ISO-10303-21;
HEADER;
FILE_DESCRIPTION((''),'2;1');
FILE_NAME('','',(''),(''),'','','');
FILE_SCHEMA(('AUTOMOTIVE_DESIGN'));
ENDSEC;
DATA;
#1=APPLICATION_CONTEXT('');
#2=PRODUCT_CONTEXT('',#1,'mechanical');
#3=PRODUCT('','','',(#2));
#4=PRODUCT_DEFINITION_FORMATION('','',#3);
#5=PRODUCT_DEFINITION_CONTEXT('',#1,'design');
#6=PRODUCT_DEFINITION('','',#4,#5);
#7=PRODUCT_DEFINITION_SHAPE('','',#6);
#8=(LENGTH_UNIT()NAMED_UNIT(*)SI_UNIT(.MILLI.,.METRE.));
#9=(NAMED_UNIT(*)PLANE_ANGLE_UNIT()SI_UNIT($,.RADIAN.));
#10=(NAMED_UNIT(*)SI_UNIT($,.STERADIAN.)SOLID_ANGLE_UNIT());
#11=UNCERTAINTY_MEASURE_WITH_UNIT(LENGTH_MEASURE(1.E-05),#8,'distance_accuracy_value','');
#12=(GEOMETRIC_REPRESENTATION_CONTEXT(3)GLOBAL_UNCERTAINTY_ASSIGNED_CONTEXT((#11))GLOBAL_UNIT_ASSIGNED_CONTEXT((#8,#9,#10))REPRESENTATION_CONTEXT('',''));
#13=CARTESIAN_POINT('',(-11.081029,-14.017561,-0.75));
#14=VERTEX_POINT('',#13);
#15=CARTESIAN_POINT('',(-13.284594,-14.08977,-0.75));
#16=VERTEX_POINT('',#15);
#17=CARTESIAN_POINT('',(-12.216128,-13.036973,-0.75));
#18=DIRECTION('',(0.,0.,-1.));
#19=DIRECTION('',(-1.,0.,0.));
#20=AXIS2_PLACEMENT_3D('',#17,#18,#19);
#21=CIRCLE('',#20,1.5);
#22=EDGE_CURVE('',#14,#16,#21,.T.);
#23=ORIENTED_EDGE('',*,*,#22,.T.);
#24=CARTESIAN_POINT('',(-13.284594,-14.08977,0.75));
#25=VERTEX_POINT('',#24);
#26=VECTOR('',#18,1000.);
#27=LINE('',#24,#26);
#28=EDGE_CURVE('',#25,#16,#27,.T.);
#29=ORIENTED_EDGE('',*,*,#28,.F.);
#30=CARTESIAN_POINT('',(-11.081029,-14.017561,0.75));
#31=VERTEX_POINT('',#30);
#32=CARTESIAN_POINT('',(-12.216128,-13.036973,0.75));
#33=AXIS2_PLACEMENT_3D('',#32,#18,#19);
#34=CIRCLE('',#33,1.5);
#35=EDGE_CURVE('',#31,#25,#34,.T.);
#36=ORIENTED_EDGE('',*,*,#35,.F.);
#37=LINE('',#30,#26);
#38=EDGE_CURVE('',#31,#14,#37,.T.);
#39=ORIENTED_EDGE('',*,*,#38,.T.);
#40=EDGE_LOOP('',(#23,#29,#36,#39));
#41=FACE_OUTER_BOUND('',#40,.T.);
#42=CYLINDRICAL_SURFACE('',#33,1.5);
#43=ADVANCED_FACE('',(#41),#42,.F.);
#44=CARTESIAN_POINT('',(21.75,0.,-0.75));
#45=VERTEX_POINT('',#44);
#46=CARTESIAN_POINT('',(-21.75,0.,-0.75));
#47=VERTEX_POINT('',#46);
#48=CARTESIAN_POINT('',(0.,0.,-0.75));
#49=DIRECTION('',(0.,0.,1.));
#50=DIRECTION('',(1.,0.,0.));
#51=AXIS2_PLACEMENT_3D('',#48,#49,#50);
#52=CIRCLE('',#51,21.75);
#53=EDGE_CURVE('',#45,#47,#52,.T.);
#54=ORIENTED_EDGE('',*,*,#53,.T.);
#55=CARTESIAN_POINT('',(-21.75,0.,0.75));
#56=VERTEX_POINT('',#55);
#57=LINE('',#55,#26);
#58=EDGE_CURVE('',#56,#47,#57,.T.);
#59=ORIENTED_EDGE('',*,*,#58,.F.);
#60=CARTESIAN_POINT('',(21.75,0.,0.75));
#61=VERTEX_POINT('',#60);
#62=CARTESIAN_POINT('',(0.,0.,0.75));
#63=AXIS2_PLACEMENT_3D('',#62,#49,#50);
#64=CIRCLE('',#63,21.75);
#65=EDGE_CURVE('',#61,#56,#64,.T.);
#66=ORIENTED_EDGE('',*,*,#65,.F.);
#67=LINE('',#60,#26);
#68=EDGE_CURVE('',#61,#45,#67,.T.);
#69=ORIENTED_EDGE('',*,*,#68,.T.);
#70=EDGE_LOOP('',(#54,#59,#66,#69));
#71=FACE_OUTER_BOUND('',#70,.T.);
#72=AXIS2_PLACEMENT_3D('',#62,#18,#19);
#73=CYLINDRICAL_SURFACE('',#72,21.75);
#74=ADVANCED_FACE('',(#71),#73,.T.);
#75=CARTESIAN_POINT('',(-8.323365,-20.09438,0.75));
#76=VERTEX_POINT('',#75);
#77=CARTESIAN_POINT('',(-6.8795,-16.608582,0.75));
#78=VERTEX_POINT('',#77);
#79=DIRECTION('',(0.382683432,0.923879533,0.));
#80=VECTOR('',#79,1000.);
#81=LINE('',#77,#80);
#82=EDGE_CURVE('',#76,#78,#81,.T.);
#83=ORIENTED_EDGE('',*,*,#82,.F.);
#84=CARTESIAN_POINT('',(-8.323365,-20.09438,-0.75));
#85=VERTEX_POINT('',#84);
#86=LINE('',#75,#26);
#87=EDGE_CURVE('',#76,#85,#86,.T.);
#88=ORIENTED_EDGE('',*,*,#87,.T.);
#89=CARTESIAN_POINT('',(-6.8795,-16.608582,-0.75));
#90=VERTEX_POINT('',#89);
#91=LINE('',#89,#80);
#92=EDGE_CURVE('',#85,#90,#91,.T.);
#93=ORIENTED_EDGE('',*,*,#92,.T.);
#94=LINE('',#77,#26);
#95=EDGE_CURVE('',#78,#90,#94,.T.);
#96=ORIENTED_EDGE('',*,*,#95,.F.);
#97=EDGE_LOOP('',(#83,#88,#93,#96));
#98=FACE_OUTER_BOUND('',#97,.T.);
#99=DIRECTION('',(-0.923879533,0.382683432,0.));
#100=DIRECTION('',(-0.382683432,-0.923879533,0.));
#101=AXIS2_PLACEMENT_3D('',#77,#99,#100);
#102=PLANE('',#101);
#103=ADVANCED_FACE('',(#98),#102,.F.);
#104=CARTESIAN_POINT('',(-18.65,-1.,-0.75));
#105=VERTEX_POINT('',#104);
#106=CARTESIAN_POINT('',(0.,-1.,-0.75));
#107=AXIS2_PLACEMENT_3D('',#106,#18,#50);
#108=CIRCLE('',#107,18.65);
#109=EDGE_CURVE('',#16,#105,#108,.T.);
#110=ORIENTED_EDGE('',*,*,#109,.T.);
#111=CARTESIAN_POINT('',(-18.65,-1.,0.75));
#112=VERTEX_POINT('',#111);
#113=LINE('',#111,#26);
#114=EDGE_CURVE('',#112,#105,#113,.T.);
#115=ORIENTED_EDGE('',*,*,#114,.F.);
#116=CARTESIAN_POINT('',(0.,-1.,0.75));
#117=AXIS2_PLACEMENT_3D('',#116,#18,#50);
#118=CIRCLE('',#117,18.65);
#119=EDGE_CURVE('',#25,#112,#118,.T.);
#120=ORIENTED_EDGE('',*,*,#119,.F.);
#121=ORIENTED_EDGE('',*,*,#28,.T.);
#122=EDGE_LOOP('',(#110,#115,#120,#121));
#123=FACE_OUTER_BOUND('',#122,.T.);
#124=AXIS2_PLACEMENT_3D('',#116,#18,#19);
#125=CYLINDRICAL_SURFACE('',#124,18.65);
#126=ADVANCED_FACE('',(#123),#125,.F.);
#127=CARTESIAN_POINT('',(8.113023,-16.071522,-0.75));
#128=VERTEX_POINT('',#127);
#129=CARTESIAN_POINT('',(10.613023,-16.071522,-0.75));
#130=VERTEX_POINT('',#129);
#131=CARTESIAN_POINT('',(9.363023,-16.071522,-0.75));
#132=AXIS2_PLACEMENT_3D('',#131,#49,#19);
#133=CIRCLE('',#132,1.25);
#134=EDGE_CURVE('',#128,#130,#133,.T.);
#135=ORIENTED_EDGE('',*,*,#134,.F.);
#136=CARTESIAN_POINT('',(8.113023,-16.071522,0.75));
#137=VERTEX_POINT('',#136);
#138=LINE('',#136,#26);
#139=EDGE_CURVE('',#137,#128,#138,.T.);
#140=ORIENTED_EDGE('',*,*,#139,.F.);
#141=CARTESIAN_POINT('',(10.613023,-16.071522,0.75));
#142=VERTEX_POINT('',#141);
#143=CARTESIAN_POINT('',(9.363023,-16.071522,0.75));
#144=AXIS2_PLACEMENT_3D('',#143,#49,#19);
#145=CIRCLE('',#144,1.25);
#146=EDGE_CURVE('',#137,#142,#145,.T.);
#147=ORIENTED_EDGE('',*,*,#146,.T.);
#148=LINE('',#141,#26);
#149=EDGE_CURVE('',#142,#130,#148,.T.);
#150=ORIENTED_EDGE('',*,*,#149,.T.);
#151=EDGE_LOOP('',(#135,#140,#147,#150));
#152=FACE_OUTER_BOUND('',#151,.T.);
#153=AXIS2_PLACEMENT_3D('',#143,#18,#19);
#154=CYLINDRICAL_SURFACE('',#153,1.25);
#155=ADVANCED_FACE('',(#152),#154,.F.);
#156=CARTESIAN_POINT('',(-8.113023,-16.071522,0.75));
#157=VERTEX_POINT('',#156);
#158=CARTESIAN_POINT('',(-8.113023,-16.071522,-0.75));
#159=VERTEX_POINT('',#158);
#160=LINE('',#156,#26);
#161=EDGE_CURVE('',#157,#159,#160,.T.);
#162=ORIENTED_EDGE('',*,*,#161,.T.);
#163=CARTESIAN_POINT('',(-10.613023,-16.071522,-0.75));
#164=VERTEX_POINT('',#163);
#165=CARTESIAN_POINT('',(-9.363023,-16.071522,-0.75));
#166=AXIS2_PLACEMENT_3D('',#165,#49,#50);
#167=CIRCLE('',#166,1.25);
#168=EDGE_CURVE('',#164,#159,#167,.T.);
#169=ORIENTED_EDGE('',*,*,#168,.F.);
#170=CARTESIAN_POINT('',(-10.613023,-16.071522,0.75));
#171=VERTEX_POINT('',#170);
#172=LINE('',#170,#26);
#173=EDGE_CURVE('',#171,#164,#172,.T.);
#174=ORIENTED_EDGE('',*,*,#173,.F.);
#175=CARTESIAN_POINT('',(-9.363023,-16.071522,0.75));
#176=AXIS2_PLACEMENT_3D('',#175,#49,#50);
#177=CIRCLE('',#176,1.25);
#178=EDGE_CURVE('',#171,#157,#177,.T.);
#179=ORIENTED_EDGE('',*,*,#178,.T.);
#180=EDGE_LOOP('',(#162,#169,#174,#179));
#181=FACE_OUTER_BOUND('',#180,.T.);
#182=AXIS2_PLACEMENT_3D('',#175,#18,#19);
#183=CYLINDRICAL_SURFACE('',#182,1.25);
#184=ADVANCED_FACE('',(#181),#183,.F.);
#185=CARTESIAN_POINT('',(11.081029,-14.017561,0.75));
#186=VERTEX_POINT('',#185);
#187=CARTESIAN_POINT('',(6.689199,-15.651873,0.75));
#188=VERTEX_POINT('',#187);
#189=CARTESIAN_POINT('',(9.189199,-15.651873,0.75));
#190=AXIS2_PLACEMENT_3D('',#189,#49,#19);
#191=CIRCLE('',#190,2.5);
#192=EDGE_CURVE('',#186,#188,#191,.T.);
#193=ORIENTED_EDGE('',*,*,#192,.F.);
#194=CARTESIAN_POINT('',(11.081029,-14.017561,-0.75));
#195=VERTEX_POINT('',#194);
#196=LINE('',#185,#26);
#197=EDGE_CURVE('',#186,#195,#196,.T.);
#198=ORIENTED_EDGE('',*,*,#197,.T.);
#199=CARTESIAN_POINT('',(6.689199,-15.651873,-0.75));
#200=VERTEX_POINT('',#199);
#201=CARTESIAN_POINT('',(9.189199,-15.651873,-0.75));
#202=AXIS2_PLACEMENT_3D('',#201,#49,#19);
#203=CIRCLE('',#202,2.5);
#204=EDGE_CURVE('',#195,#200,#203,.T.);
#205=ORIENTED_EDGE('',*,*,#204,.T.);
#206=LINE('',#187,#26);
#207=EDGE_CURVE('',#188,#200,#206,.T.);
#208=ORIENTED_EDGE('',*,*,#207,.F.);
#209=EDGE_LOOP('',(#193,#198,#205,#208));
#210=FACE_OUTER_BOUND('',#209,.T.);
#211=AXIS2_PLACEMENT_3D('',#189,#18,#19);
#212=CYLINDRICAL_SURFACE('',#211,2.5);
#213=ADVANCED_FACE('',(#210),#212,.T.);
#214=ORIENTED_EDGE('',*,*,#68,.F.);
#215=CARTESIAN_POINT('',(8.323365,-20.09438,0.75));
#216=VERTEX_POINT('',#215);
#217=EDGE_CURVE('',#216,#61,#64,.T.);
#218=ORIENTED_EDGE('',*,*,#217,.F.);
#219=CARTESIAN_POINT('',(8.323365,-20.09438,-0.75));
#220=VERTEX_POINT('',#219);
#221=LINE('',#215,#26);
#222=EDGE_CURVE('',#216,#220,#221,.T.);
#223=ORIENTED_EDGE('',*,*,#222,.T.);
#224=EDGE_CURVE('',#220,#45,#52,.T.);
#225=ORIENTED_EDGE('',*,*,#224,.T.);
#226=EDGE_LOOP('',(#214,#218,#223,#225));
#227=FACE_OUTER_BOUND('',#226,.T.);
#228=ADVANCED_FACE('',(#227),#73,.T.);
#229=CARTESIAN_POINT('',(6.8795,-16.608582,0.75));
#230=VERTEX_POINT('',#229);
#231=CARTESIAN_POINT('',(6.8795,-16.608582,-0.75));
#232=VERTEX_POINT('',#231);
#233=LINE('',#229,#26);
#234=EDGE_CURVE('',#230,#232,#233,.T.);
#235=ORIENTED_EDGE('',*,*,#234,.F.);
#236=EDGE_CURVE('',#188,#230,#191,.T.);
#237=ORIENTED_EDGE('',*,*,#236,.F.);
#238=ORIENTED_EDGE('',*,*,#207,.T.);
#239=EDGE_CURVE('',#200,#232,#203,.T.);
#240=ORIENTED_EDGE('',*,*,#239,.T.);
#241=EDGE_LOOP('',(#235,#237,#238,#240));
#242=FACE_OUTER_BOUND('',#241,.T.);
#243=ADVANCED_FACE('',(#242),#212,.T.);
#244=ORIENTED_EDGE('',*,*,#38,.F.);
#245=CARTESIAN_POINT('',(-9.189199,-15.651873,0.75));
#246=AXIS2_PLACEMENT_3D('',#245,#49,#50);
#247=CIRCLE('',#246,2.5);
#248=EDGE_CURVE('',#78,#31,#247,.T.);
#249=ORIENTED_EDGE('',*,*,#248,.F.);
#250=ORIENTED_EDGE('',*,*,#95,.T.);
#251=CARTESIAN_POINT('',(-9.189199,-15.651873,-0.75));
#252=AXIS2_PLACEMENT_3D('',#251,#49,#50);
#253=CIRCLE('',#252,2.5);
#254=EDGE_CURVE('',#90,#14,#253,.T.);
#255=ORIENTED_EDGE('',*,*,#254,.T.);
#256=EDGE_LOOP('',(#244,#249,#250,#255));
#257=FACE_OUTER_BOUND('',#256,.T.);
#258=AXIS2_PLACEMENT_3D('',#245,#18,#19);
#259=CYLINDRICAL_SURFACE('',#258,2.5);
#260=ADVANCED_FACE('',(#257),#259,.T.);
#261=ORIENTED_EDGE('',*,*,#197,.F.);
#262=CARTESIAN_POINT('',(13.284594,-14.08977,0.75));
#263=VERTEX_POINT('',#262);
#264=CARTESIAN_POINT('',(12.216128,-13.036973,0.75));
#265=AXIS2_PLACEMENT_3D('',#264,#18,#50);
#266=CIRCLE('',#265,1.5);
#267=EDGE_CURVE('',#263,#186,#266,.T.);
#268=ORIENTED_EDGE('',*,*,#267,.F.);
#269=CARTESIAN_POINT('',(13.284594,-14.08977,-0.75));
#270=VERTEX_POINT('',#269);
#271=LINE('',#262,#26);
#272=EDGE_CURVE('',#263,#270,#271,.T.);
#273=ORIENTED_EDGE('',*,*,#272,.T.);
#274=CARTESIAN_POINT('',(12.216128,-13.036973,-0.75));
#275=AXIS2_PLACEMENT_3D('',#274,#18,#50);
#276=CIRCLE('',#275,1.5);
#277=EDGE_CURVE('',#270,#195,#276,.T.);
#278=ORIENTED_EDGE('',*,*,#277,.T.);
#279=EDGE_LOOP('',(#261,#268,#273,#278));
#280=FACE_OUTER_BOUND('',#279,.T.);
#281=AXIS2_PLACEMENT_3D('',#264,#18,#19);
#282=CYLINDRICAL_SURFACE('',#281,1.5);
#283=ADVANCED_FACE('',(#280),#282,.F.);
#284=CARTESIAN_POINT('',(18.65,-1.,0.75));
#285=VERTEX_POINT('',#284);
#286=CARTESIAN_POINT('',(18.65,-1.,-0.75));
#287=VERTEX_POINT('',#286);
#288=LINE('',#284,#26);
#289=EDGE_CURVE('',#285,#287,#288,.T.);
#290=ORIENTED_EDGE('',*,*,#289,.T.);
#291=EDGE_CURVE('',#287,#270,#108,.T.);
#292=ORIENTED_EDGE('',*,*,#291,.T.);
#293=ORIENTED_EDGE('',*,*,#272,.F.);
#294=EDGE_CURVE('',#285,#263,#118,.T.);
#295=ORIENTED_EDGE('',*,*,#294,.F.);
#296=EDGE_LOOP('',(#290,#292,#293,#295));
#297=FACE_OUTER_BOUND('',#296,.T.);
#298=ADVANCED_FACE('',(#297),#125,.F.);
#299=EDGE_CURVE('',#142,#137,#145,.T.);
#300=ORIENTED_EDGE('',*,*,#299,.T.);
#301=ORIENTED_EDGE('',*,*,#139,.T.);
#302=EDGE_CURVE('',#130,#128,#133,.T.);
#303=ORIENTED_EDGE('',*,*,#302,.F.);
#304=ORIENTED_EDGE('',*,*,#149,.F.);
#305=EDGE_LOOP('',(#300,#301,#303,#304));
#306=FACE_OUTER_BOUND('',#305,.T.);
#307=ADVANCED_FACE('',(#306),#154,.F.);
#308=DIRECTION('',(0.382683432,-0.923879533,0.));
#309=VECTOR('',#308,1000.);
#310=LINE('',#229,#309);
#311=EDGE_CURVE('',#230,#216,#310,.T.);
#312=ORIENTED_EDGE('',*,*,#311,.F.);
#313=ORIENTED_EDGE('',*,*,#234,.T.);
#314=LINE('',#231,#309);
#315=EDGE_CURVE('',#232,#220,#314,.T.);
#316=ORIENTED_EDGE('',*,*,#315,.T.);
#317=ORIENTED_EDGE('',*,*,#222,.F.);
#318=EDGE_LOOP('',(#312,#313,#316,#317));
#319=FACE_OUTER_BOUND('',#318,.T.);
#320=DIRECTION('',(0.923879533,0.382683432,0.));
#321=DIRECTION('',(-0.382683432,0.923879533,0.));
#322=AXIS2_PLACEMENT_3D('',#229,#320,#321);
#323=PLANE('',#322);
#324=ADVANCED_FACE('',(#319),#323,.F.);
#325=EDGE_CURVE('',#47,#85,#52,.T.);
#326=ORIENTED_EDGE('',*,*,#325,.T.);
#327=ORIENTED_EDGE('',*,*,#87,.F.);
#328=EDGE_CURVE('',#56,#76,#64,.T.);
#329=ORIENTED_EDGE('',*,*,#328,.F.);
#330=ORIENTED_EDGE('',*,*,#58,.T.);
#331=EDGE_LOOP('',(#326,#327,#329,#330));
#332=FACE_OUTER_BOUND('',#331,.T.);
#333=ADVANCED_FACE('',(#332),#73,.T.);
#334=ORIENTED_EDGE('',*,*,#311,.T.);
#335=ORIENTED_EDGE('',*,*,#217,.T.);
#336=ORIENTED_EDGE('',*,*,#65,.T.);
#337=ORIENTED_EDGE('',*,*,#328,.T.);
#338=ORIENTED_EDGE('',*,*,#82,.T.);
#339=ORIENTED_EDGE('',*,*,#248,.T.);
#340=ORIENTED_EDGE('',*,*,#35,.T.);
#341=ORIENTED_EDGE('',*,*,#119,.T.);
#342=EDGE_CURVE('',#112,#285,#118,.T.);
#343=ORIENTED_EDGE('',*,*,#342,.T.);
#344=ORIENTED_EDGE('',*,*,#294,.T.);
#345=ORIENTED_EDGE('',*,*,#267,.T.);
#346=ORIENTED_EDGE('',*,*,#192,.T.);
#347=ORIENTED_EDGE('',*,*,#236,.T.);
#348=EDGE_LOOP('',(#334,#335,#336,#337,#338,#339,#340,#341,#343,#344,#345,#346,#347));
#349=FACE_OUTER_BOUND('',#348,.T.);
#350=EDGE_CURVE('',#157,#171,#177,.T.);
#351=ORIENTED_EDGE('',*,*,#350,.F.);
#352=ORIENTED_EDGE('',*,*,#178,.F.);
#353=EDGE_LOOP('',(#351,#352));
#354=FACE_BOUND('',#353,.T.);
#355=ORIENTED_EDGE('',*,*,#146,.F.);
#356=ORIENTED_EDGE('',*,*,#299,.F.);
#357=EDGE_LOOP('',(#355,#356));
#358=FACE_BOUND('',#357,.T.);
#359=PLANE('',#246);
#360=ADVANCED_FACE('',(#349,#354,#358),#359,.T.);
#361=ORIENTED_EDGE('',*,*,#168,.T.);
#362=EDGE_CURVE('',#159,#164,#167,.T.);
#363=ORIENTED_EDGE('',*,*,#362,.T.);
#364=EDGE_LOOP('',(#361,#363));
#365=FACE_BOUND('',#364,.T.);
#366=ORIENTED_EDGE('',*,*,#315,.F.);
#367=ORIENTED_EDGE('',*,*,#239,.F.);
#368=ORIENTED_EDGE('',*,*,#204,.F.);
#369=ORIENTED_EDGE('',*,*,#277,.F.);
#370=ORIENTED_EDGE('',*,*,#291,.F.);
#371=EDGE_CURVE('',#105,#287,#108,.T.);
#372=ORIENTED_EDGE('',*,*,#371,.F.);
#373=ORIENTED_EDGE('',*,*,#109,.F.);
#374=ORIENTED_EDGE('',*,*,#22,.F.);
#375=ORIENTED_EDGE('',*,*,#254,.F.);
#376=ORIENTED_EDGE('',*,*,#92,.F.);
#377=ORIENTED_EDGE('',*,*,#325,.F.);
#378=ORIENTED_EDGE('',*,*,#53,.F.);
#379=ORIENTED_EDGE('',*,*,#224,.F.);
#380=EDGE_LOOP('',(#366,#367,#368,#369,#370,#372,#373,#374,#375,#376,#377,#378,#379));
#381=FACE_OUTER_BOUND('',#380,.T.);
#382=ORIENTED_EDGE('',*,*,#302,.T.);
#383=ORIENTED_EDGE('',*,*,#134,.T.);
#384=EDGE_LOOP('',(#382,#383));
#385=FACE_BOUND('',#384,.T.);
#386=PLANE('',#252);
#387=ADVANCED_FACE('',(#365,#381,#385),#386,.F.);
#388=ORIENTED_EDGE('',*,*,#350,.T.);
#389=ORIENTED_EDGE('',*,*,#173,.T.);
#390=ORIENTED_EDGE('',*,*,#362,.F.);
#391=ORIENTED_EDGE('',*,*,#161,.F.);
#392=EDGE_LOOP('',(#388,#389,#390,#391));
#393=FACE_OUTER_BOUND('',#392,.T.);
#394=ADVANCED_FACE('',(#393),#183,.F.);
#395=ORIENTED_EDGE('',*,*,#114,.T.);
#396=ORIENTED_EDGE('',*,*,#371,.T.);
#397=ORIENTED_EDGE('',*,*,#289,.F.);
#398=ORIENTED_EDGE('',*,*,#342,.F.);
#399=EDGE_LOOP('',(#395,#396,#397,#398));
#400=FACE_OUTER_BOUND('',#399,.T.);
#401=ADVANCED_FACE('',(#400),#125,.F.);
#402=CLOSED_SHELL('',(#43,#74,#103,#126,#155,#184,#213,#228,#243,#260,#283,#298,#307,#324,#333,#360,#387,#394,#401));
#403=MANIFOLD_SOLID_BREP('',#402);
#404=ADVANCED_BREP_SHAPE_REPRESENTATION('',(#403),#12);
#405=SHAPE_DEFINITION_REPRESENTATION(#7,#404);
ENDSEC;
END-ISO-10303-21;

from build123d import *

# Parameters (mm, degrees)
EXTRUDE_962_DEPTH      = 0.75
EXTRUDE_962_DEPTH_BACK = 0.75
SKETCH_1_R             = 1.25


with BuildPart() as part:
    # 草图1 → Extrude 962 (new, two sides: drawn at the far end of the back side and taken through both)
    with BuildSketch(Plane.XY.offset(-EXTRUDE_962_DEPTH_BACK)):
        with BuildLine():
            Line((-6.879499755, -16.608581611), (-8.323364654, -20.094379832))
            ThreePointArc((-8.323364654, -20.094379832), (0, 21.75), (8.323364654, -20.094379832))
            Line((8.323364654, -20.094379832), (6.879499755, -16.608581611))
            ThreePointArc((6.879499755, -16.608581611), (7.876948304, -13.523963446), (11.081029231, -14.017560694))
            ThreePointArc((11.081029231, -14.017560694), (12.16700015, -14.536168573), (13.28459359, -14.08976979))
            ThreePointArc((13.28459359, -14.08976979), (0, 17.65), (-13.28459359, -14.08976979))
            ThreePointArc((-13.28459359, -14.08976979), (-12.16700015, -14.536168573), (-11.081029231, -14.017560694))
            ThreePointArc((-11.081029231, -14.017560694), (-7.876948304, -13.523963446), (-6.879499755, -16.608581611))
        make_face()
        with Locations((-9.363022706, -16.071521577)):
            Circle(SKETCH_1_R, mode=Mode.SUBTRACT)
        with Locations(Location((9.363022706, -16.071521577, 0), (0, 0, 180))):
            Circle(SKETCH_1_R, mode=Mode.SUBTRACT)
    extrude(amount=EXTRUDE_962_DEPTH + EXTRUDE_962_DEPTH_BACK)


solid = part.part
